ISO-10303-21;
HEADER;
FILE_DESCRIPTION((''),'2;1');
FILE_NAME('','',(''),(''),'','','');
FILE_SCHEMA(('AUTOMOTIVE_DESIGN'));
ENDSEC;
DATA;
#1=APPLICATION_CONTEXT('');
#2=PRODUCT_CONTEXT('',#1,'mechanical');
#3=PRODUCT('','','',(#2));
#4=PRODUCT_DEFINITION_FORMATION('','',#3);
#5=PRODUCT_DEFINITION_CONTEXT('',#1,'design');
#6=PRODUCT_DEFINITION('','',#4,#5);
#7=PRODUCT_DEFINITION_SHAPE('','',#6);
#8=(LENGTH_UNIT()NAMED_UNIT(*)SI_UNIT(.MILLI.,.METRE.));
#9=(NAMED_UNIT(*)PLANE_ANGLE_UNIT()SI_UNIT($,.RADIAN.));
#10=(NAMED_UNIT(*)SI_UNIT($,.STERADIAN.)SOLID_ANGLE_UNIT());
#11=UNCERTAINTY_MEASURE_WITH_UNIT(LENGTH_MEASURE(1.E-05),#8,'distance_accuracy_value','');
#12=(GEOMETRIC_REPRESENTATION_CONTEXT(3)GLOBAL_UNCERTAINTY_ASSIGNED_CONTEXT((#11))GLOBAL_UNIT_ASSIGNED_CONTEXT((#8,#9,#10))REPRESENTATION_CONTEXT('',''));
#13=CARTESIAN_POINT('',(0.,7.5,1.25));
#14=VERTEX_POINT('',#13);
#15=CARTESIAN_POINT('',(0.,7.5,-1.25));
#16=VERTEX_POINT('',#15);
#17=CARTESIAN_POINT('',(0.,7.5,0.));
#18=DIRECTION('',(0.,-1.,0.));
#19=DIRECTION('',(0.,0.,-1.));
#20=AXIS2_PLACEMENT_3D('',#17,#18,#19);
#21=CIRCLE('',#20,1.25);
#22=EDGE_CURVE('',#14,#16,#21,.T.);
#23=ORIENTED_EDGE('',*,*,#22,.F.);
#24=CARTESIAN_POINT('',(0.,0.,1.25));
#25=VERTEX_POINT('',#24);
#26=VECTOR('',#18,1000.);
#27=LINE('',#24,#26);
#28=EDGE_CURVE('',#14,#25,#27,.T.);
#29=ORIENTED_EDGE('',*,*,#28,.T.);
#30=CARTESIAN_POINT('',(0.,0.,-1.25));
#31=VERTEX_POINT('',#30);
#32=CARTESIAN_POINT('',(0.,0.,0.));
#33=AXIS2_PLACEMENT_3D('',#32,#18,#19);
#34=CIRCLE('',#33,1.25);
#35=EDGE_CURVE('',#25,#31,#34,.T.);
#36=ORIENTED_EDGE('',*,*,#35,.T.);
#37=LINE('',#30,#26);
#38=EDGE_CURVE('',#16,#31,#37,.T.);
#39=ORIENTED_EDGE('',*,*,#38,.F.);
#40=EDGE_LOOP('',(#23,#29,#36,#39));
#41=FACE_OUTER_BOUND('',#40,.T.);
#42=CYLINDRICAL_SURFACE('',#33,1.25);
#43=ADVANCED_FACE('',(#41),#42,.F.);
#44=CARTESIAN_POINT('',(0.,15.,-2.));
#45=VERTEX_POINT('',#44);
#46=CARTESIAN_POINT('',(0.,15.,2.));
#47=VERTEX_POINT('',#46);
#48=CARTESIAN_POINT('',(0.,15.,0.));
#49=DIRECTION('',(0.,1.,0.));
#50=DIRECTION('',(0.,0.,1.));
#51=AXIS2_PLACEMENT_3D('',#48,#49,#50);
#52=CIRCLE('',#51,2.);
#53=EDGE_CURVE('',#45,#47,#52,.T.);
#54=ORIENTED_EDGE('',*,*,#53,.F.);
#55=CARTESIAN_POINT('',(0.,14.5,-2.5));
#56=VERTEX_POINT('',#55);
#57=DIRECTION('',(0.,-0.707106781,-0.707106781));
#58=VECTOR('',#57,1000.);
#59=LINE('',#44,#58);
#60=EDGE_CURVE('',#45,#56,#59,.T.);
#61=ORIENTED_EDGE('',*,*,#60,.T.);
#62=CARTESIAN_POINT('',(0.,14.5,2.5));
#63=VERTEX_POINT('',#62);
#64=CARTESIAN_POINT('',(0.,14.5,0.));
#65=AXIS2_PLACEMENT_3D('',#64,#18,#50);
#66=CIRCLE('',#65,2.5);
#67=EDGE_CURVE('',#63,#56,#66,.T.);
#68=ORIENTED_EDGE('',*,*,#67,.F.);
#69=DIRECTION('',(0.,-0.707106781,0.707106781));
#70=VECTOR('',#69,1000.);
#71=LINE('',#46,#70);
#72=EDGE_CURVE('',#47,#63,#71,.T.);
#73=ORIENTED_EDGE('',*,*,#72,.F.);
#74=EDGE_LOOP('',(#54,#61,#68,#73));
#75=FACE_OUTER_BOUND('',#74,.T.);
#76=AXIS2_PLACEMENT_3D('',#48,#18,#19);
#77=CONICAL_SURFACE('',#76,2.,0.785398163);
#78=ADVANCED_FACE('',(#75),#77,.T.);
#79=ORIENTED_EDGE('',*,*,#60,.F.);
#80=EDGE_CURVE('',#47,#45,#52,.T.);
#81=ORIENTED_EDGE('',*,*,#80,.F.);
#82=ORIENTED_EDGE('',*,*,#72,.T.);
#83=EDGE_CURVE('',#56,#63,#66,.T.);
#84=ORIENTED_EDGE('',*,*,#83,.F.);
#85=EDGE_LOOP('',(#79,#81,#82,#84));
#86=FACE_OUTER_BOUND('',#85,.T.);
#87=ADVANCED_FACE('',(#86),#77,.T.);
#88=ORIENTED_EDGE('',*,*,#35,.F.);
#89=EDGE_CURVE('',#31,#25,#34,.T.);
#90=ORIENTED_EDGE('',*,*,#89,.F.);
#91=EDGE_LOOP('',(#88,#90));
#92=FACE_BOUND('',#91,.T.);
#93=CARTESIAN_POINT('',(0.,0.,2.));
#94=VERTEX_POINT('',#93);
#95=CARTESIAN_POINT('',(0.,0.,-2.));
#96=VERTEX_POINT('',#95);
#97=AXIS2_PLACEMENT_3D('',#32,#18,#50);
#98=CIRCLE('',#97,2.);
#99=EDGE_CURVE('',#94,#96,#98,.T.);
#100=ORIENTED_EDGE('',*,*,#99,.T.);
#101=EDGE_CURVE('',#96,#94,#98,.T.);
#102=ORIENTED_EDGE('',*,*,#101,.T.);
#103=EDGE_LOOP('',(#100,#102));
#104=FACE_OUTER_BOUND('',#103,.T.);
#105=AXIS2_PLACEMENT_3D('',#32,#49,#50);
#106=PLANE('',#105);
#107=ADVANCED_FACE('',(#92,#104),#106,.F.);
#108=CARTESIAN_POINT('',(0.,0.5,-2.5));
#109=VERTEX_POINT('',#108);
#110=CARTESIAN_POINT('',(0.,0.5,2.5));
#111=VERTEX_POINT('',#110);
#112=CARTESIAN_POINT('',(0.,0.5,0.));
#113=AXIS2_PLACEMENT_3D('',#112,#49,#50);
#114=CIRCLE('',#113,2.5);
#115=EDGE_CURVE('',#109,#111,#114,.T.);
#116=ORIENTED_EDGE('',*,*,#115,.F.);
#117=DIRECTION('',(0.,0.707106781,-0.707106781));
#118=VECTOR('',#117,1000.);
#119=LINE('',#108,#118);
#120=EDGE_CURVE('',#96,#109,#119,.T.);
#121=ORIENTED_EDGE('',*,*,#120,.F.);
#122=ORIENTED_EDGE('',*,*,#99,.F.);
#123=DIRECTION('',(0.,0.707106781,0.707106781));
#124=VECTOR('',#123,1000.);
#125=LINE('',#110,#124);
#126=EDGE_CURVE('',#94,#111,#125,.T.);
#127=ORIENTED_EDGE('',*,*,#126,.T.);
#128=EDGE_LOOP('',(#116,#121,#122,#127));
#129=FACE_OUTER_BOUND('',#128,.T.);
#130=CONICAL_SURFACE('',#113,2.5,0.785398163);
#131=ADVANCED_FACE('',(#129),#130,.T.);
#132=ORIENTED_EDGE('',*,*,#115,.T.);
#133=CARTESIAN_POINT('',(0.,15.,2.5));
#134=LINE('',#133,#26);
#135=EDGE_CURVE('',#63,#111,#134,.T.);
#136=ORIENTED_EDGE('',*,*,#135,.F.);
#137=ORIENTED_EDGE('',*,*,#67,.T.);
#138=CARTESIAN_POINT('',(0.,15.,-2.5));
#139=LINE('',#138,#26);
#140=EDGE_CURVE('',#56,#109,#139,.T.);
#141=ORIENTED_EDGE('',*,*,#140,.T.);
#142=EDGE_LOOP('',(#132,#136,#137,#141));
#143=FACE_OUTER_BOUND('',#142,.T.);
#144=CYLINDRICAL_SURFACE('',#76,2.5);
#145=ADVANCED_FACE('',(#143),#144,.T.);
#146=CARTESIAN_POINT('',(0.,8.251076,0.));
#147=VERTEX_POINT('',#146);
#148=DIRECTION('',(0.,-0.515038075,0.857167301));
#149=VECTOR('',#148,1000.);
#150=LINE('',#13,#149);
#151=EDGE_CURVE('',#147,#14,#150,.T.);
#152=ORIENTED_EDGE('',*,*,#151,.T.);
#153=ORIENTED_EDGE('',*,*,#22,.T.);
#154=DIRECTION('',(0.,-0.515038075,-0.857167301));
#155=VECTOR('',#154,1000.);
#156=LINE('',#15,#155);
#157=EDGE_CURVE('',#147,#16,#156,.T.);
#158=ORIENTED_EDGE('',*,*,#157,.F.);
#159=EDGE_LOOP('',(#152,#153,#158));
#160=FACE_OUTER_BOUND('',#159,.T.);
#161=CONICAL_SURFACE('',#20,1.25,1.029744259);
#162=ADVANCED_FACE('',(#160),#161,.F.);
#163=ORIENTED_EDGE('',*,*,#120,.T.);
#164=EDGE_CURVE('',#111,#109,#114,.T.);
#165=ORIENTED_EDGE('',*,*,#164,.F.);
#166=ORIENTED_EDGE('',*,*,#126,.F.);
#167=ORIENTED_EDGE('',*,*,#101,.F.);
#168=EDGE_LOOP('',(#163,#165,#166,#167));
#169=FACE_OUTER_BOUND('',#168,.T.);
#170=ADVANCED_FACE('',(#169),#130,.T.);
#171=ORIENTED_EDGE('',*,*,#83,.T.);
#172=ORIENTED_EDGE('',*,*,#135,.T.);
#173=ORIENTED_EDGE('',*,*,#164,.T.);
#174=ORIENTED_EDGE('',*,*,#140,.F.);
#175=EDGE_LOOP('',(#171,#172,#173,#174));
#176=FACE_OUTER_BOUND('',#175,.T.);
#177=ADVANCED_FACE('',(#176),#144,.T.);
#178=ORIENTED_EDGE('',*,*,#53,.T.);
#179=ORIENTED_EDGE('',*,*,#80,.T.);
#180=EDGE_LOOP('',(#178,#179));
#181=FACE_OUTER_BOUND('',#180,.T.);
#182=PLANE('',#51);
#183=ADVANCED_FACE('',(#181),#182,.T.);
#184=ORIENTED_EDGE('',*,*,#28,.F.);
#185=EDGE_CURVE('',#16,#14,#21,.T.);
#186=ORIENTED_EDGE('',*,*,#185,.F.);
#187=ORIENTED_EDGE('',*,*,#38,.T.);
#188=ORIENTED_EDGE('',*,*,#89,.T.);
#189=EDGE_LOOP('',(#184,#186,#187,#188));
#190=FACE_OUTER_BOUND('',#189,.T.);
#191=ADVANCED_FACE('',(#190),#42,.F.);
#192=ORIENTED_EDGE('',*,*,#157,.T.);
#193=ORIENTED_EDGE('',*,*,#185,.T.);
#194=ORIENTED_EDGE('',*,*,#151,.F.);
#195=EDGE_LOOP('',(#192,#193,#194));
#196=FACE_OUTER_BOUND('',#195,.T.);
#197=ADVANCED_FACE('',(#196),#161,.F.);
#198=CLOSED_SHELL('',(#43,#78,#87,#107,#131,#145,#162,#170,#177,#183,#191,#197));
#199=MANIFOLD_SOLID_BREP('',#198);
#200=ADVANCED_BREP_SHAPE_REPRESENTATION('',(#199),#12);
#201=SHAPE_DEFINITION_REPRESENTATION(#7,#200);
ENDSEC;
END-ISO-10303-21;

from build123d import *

# Parameters (mm, degrees)
SKETCH_1_R             = 2.5
EXTRUDE_1_DEPTH        = 15
HOLE_WIZARD_M3_1_D     = 2.5
HOLE_WIZARD_M3_1_DEPTH = 7.5
HOLE_WIZARD_M3_1_TIP   = 0.751075774
CHAMFER_1_SIZE         = 0.5


with BuildPart() as part:
    # 草图1 → 凸台-拉伸1 (new body)
    with BuildSketch(Plane(origin=(0, 0, 0), x_dir=(1, 0, 0), z_dir=(0, 1, 0))):
        with Locations(Location((0, 0, 0), (0, 0, 270))):
            Circle(SKETCH_1_R)
    extrude(amount=EXTRUDE_1_DEPTH)

    # M3 螺纹孔1
    with Locations(Plane(origin=(0, 0, 0), x_dir=(-1, 0, 0), z_dir=(0, -1, 0))):
        with Locations((0, 0)):
            Hole(HOLE_WIZARD_M3_1_D / 2, depth=HOLE_WIZARD_M3_1_DEPTH)
            with Locations((0, 0, -(HOLE_WIZARD_M3_1_DEPTH + HOLE_WIZARD_M3_1_TIP / 2))):  # 118° drill point
                Cone(0, HOLE_WIZARD_M3_1_D / 2, HOLE_WIZARD_M3_1_TIP, mode=Mode.SUBTRACT)

    # 倒角1
    chamfer_1_edges = [part.edges().sort_by_distance(p)[0] for p in [
        (0, 0, -2.5),
        (0, 15, -2.5),
    ]]
    chamfer(chamfer_1_edges, length=CHAMFER_1_SIZE)


solid = part.part
